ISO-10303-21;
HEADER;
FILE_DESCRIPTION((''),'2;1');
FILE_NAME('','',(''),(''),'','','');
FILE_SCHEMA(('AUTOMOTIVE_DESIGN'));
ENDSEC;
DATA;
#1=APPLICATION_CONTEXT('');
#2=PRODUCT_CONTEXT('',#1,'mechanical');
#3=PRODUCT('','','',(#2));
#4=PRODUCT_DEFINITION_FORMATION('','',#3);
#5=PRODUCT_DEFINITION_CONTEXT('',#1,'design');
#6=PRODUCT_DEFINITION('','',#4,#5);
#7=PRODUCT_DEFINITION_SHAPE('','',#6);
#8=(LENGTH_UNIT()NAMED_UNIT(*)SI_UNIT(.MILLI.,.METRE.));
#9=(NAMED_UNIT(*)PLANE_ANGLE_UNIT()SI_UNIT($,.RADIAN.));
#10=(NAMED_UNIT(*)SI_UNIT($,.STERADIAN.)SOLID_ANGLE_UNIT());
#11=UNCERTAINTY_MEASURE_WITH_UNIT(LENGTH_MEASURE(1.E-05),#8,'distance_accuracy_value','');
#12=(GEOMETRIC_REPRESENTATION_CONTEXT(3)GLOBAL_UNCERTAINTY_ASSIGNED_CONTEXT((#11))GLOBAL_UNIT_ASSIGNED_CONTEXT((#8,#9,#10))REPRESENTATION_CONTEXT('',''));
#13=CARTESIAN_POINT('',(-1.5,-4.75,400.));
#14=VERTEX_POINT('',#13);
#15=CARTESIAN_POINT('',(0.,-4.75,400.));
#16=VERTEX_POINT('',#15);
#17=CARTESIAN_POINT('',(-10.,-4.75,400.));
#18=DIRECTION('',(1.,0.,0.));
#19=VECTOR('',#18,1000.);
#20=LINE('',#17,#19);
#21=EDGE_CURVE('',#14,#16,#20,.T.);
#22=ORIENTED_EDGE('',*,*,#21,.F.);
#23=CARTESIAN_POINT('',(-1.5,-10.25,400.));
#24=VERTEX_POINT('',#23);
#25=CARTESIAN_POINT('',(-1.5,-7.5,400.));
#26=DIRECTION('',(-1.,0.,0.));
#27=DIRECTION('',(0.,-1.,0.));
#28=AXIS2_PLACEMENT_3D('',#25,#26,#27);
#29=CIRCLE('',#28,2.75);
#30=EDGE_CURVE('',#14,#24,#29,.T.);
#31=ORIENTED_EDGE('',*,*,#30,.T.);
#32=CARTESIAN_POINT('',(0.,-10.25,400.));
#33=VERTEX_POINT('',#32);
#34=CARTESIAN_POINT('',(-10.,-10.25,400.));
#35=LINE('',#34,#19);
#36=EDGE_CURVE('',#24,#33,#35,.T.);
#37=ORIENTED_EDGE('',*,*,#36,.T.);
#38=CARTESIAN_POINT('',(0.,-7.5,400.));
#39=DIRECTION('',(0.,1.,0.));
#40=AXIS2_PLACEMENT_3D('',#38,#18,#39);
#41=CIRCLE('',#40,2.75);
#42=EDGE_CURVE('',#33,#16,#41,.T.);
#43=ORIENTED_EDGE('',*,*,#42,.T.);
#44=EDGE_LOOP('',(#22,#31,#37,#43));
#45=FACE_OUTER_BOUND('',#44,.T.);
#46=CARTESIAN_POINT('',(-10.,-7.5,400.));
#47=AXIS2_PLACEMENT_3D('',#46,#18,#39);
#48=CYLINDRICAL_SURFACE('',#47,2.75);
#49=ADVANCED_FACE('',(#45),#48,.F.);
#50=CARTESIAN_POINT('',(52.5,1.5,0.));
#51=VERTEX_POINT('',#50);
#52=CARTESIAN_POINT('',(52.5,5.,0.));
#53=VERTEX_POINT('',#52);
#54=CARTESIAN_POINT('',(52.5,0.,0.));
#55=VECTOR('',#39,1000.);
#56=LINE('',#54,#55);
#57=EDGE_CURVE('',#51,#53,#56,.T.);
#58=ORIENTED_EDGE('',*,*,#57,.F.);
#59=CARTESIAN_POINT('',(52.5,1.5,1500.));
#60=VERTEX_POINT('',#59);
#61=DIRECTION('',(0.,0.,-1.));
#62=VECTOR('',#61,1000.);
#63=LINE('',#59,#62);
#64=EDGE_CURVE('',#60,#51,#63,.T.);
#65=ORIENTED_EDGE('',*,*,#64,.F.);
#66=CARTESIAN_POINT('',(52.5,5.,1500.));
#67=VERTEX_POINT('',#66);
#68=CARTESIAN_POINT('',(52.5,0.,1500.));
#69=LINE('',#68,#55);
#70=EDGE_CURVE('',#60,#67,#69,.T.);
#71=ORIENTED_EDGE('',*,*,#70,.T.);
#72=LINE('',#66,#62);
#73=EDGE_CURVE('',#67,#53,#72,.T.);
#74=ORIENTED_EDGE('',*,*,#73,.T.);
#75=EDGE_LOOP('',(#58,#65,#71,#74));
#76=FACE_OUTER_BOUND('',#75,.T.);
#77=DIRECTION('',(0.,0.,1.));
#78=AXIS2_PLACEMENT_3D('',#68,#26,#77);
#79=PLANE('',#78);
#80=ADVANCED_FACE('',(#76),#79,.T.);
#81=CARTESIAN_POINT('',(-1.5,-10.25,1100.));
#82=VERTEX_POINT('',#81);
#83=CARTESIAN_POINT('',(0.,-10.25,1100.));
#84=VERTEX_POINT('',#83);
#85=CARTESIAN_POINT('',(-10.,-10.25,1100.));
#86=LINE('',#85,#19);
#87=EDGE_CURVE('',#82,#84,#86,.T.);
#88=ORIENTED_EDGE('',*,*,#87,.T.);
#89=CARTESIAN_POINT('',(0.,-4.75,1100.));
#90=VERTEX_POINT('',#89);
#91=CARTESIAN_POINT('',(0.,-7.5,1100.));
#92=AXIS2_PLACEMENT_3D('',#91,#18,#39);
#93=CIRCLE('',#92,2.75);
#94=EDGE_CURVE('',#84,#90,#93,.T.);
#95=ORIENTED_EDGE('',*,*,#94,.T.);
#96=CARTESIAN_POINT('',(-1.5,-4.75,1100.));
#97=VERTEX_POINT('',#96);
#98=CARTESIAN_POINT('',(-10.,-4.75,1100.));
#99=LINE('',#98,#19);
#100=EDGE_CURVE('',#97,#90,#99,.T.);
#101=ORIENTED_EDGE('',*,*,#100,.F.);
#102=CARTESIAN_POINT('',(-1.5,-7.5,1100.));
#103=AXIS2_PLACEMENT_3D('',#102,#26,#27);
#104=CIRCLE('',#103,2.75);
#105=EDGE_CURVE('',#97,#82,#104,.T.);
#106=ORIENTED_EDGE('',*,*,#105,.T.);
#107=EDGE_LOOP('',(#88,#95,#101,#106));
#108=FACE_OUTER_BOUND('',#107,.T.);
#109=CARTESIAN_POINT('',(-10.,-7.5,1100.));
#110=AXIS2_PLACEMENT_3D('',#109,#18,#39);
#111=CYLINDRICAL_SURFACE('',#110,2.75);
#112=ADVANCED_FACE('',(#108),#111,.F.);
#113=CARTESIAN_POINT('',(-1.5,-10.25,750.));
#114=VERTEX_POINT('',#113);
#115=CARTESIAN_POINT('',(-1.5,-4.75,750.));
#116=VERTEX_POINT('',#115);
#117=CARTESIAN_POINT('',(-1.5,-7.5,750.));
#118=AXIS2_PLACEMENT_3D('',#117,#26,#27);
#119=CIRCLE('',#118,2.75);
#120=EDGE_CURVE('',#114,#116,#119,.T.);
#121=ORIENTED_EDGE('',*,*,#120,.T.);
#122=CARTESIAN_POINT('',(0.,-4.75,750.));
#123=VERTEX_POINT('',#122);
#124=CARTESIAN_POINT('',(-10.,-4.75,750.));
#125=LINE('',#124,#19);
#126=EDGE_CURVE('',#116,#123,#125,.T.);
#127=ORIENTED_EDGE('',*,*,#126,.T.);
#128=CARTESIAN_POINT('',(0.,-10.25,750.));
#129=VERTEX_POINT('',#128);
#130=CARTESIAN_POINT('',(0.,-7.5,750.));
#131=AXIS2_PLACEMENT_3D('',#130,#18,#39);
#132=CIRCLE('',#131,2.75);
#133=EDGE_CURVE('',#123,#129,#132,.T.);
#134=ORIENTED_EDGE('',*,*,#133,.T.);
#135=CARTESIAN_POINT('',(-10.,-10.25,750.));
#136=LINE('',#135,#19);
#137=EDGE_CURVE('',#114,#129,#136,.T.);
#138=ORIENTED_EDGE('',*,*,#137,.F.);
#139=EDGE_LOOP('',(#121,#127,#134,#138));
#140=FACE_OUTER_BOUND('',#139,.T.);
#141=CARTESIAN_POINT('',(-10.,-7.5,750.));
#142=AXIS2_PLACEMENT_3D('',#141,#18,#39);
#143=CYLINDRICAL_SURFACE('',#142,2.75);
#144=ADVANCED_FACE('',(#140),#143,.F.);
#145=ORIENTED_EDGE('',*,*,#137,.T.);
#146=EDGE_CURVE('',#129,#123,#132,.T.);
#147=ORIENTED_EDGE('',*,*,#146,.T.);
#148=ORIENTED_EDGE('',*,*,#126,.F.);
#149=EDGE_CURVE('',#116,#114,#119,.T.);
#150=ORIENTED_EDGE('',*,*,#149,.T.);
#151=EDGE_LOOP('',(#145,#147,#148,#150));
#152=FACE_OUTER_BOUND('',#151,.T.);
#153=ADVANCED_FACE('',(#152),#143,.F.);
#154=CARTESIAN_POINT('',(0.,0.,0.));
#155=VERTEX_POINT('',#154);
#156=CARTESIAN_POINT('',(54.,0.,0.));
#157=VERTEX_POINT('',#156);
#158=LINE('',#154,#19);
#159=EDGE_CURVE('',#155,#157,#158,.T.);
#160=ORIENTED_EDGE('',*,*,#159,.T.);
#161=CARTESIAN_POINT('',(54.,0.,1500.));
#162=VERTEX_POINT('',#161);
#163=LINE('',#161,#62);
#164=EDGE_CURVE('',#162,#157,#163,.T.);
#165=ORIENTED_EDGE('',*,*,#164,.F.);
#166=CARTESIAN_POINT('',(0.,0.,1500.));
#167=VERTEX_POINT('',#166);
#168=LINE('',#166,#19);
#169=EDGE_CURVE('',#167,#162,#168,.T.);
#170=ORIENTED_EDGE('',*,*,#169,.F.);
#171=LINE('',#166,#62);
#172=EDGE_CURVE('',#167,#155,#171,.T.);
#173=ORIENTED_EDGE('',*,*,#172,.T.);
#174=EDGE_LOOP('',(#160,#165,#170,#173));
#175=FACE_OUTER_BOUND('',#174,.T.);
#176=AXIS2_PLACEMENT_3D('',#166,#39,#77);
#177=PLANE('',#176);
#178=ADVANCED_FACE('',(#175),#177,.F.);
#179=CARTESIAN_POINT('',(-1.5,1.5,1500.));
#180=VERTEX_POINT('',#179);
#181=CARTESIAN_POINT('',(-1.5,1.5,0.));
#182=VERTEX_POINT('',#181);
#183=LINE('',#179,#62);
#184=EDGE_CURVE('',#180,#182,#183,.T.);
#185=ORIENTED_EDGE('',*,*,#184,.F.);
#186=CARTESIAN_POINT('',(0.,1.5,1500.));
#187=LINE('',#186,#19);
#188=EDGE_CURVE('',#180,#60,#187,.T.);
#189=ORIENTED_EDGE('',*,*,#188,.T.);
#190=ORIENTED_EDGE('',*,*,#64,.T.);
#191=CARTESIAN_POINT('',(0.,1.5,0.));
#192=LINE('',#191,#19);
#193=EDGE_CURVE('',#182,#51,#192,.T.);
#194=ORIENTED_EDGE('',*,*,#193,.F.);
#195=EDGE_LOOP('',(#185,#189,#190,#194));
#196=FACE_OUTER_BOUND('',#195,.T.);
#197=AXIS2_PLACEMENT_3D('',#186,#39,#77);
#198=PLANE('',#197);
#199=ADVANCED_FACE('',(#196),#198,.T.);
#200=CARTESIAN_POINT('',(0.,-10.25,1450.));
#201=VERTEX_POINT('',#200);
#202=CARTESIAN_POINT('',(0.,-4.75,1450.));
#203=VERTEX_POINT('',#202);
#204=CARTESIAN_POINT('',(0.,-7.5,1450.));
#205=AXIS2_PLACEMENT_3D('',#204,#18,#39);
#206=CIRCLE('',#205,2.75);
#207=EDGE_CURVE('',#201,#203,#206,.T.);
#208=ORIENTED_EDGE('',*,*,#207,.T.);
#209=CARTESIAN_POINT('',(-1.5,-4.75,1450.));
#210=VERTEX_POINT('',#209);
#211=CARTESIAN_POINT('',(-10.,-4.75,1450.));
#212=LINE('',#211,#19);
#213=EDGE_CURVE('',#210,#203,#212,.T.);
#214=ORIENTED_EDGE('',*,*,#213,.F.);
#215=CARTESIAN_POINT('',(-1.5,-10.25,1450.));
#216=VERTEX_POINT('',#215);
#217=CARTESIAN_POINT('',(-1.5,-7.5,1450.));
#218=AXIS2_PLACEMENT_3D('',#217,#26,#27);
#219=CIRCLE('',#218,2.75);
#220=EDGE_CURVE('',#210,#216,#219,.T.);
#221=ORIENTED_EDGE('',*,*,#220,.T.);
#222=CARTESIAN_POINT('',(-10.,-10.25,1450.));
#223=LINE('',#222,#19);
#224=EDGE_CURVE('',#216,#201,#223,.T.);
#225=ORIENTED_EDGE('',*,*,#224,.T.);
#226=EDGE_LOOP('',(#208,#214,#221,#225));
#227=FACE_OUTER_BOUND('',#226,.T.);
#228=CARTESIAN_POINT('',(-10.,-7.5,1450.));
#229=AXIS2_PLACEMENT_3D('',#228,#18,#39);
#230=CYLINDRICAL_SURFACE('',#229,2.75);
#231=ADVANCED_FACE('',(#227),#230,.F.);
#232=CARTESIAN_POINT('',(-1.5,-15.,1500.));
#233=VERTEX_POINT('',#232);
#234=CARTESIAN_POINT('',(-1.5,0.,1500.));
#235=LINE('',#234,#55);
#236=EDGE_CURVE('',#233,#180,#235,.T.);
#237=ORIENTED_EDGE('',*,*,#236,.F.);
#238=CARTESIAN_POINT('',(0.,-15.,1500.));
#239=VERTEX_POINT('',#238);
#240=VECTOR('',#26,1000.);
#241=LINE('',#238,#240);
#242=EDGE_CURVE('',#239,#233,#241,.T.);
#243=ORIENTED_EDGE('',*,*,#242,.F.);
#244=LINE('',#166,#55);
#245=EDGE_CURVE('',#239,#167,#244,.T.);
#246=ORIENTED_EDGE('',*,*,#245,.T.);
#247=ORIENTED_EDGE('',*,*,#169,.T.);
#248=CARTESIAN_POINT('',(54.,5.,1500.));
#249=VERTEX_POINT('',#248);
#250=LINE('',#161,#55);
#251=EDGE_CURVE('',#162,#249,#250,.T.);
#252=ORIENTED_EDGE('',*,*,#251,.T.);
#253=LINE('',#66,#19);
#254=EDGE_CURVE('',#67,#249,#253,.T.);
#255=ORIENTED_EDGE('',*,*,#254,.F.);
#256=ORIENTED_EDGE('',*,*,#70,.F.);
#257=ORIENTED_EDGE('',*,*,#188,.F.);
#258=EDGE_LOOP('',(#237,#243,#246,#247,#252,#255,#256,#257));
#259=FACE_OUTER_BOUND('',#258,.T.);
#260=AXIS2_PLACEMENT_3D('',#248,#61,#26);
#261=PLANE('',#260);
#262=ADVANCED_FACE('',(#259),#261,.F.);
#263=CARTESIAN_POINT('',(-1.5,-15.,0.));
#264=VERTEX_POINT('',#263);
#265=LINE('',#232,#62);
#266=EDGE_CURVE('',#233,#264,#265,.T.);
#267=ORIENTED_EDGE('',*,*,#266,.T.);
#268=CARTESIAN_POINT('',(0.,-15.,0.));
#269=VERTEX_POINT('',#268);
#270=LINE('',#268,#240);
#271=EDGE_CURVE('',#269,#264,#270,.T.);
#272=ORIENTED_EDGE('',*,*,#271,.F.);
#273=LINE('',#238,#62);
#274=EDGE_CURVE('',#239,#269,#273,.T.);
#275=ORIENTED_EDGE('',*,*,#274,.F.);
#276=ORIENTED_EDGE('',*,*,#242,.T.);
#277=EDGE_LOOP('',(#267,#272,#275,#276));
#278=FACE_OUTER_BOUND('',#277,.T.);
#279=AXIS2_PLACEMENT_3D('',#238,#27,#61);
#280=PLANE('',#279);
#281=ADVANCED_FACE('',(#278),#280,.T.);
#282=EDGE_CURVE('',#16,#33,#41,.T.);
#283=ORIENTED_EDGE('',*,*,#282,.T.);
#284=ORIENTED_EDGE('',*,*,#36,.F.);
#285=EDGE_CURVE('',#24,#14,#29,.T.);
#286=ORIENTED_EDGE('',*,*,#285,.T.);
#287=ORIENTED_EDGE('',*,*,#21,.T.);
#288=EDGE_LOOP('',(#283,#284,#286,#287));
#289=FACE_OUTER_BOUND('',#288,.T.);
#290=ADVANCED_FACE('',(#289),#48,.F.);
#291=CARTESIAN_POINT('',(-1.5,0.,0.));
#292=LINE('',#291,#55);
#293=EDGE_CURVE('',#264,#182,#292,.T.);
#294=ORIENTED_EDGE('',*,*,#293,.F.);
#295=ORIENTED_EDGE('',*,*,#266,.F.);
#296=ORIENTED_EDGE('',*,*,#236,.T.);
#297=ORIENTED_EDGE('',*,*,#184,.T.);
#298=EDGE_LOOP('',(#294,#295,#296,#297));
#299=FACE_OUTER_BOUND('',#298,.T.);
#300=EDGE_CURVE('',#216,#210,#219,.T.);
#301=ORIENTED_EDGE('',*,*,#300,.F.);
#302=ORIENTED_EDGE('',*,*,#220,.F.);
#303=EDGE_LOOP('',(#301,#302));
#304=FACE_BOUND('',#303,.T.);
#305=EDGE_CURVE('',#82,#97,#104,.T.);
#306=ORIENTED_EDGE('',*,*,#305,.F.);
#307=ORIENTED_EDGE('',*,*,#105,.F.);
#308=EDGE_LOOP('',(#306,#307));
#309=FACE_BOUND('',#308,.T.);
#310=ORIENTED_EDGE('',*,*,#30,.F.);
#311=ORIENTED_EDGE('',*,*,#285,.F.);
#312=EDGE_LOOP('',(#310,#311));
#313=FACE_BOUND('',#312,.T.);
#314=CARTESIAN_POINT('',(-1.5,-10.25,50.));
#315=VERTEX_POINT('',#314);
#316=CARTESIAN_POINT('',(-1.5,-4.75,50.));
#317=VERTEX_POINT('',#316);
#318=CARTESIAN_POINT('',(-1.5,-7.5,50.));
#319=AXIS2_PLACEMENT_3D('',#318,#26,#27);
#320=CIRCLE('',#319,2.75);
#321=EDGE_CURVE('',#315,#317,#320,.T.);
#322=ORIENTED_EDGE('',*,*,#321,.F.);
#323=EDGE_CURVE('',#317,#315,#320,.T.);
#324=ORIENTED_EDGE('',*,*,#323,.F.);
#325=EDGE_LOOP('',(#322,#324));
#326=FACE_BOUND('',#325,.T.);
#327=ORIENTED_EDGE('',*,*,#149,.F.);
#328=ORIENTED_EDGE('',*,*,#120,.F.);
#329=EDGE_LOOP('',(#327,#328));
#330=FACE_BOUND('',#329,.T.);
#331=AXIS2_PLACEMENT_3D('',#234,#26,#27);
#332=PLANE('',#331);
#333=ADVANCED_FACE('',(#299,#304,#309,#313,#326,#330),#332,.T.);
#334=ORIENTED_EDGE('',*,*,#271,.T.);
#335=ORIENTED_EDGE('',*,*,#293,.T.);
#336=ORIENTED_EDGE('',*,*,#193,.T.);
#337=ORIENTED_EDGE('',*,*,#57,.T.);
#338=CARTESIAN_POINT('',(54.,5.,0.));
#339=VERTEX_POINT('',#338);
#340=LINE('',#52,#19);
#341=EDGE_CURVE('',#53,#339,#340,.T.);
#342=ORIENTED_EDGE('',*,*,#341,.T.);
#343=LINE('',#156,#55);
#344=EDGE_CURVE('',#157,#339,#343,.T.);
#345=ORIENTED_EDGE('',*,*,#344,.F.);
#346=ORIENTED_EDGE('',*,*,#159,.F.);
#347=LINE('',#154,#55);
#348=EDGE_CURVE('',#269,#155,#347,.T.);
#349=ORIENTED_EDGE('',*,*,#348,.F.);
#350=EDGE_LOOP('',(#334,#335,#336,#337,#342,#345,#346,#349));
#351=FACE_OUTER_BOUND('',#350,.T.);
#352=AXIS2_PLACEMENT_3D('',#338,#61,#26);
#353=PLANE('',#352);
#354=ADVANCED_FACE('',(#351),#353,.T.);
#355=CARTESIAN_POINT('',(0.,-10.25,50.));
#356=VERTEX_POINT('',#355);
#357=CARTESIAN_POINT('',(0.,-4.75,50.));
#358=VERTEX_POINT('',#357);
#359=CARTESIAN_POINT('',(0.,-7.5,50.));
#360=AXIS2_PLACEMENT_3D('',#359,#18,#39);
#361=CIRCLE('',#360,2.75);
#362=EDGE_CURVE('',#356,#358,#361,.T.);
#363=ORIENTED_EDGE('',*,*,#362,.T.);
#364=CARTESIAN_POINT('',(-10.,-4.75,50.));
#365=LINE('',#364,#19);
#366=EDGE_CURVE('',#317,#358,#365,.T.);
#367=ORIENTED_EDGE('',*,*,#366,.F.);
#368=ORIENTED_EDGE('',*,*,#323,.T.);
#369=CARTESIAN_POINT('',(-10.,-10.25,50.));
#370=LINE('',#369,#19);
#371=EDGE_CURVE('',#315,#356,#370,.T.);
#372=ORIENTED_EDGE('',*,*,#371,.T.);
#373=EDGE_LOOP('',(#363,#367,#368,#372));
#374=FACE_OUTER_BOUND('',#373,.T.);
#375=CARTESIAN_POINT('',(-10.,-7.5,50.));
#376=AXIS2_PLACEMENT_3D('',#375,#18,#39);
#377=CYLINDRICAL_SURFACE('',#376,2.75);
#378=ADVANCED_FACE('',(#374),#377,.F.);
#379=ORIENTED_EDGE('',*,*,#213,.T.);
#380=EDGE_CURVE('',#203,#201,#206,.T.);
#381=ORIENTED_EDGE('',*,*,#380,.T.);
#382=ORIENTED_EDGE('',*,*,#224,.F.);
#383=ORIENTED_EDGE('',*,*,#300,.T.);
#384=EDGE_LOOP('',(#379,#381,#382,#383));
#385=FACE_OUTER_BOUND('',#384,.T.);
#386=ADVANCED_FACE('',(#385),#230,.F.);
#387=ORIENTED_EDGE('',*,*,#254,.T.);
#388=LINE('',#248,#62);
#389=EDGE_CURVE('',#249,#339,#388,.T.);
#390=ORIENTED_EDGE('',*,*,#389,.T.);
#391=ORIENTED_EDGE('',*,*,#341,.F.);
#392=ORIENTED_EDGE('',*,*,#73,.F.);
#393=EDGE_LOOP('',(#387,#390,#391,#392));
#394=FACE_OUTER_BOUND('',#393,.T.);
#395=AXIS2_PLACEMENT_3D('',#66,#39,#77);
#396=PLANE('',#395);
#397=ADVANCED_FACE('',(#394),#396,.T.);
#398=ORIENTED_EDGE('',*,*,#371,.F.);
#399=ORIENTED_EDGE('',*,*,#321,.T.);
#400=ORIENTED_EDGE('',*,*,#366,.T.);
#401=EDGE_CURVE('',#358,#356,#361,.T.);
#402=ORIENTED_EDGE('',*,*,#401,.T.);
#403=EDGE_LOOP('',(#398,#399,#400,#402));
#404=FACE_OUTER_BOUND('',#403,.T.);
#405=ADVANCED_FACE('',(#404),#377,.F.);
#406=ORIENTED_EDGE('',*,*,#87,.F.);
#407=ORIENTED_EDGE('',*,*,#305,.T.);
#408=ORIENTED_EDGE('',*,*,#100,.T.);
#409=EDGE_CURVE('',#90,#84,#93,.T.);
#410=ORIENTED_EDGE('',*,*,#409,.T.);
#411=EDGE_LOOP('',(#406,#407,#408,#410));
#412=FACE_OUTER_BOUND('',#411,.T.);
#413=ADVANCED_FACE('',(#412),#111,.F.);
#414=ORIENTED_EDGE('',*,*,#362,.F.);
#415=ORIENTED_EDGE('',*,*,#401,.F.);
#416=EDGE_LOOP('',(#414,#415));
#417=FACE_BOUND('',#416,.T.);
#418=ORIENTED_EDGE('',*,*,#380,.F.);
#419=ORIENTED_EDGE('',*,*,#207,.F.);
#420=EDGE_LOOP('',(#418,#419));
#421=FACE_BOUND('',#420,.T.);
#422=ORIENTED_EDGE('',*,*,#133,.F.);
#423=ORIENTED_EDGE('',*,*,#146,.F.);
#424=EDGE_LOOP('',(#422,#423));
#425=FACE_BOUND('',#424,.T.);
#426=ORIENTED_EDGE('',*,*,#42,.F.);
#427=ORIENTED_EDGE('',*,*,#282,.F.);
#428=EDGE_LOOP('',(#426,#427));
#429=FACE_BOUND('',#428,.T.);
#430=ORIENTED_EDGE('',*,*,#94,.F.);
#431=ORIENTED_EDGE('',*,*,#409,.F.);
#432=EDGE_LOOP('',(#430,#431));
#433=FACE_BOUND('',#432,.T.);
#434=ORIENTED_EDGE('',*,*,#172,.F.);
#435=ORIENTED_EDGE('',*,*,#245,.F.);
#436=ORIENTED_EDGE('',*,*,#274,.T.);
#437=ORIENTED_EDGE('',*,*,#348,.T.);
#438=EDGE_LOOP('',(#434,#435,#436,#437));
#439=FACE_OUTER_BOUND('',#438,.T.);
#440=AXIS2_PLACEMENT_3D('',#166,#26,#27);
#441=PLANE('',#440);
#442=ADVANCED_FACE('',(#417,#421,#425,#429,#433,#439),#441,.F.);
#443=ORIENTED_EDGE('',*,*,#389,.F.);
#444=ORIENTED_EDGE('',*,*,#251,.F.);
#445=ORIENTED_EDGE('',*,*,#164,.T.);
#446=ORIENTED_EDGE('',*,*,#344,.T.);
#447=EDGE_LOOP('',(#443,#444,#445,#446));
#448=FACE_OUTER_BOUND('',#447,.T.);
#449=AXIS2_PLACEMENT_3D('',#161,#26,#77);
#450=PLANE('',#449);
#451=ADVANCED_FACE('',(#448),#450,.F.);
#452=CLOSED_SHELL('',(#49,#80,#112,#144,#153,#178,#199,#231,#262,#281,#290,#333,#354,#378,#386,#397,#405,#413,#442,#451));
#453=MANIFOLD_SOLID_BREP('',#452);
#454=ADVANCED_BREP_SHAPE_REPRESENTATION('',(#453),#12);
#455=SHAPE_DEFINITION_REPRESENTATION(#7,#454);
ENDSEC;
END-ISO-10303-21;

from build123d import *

# Parameters (mm, degrees)
EXTRUDE_1_DEPTH     = 1500
SKETCH_2_R          = 2.75
CUT_EXTRUDE_1_DEPTH = 10


with BuildPart() as part:
    # 草图1 → 拉伸-薄壁1 (new body)
    with BuildSketch(Plane.XY):
        Polygon((54, 5), (54, 0), (0, 0), (0, -15), (-1.5, -15), (-1.5, 1.5), (52.5, 1.5), (52.5, 5), align=None)
    extrude(amount=EXTRUDE_1_DEPTH)

    # 草图2 → 切除-拉伸1 (cut)
    with BuildSketch(Plane(origin=(0, 0, 0), x_dir=(0, 0, -1), z_dir=(1, 0, 0))):
        with Locations(Location((-1450, -7.5, 0), (0, 0, 90))):
            Circle(SKETCH_2_R)
        with Locations(Location((-1100, -7.5, 0), (0, 0, 90))):
            Circle(SKETCH_2_R)
        with Locations(Location((-750, -7.5, 0), (0, 0, 90))):
            Circle(SKETCH_2_R)
        with Locations(Location((-400, -7.5, 0), (0, 0, 90))):
            Circle(SKETCH_2_R)
        with Locations(Location((-50, -7.5, 0), (0, 0, 90))):
            Circle(SKETCH_2_R)
    extrude(amount=-CUT_EXTRUDE_1_DEPTH, mode=Mode.SUBTRACT)


solid = part.part
